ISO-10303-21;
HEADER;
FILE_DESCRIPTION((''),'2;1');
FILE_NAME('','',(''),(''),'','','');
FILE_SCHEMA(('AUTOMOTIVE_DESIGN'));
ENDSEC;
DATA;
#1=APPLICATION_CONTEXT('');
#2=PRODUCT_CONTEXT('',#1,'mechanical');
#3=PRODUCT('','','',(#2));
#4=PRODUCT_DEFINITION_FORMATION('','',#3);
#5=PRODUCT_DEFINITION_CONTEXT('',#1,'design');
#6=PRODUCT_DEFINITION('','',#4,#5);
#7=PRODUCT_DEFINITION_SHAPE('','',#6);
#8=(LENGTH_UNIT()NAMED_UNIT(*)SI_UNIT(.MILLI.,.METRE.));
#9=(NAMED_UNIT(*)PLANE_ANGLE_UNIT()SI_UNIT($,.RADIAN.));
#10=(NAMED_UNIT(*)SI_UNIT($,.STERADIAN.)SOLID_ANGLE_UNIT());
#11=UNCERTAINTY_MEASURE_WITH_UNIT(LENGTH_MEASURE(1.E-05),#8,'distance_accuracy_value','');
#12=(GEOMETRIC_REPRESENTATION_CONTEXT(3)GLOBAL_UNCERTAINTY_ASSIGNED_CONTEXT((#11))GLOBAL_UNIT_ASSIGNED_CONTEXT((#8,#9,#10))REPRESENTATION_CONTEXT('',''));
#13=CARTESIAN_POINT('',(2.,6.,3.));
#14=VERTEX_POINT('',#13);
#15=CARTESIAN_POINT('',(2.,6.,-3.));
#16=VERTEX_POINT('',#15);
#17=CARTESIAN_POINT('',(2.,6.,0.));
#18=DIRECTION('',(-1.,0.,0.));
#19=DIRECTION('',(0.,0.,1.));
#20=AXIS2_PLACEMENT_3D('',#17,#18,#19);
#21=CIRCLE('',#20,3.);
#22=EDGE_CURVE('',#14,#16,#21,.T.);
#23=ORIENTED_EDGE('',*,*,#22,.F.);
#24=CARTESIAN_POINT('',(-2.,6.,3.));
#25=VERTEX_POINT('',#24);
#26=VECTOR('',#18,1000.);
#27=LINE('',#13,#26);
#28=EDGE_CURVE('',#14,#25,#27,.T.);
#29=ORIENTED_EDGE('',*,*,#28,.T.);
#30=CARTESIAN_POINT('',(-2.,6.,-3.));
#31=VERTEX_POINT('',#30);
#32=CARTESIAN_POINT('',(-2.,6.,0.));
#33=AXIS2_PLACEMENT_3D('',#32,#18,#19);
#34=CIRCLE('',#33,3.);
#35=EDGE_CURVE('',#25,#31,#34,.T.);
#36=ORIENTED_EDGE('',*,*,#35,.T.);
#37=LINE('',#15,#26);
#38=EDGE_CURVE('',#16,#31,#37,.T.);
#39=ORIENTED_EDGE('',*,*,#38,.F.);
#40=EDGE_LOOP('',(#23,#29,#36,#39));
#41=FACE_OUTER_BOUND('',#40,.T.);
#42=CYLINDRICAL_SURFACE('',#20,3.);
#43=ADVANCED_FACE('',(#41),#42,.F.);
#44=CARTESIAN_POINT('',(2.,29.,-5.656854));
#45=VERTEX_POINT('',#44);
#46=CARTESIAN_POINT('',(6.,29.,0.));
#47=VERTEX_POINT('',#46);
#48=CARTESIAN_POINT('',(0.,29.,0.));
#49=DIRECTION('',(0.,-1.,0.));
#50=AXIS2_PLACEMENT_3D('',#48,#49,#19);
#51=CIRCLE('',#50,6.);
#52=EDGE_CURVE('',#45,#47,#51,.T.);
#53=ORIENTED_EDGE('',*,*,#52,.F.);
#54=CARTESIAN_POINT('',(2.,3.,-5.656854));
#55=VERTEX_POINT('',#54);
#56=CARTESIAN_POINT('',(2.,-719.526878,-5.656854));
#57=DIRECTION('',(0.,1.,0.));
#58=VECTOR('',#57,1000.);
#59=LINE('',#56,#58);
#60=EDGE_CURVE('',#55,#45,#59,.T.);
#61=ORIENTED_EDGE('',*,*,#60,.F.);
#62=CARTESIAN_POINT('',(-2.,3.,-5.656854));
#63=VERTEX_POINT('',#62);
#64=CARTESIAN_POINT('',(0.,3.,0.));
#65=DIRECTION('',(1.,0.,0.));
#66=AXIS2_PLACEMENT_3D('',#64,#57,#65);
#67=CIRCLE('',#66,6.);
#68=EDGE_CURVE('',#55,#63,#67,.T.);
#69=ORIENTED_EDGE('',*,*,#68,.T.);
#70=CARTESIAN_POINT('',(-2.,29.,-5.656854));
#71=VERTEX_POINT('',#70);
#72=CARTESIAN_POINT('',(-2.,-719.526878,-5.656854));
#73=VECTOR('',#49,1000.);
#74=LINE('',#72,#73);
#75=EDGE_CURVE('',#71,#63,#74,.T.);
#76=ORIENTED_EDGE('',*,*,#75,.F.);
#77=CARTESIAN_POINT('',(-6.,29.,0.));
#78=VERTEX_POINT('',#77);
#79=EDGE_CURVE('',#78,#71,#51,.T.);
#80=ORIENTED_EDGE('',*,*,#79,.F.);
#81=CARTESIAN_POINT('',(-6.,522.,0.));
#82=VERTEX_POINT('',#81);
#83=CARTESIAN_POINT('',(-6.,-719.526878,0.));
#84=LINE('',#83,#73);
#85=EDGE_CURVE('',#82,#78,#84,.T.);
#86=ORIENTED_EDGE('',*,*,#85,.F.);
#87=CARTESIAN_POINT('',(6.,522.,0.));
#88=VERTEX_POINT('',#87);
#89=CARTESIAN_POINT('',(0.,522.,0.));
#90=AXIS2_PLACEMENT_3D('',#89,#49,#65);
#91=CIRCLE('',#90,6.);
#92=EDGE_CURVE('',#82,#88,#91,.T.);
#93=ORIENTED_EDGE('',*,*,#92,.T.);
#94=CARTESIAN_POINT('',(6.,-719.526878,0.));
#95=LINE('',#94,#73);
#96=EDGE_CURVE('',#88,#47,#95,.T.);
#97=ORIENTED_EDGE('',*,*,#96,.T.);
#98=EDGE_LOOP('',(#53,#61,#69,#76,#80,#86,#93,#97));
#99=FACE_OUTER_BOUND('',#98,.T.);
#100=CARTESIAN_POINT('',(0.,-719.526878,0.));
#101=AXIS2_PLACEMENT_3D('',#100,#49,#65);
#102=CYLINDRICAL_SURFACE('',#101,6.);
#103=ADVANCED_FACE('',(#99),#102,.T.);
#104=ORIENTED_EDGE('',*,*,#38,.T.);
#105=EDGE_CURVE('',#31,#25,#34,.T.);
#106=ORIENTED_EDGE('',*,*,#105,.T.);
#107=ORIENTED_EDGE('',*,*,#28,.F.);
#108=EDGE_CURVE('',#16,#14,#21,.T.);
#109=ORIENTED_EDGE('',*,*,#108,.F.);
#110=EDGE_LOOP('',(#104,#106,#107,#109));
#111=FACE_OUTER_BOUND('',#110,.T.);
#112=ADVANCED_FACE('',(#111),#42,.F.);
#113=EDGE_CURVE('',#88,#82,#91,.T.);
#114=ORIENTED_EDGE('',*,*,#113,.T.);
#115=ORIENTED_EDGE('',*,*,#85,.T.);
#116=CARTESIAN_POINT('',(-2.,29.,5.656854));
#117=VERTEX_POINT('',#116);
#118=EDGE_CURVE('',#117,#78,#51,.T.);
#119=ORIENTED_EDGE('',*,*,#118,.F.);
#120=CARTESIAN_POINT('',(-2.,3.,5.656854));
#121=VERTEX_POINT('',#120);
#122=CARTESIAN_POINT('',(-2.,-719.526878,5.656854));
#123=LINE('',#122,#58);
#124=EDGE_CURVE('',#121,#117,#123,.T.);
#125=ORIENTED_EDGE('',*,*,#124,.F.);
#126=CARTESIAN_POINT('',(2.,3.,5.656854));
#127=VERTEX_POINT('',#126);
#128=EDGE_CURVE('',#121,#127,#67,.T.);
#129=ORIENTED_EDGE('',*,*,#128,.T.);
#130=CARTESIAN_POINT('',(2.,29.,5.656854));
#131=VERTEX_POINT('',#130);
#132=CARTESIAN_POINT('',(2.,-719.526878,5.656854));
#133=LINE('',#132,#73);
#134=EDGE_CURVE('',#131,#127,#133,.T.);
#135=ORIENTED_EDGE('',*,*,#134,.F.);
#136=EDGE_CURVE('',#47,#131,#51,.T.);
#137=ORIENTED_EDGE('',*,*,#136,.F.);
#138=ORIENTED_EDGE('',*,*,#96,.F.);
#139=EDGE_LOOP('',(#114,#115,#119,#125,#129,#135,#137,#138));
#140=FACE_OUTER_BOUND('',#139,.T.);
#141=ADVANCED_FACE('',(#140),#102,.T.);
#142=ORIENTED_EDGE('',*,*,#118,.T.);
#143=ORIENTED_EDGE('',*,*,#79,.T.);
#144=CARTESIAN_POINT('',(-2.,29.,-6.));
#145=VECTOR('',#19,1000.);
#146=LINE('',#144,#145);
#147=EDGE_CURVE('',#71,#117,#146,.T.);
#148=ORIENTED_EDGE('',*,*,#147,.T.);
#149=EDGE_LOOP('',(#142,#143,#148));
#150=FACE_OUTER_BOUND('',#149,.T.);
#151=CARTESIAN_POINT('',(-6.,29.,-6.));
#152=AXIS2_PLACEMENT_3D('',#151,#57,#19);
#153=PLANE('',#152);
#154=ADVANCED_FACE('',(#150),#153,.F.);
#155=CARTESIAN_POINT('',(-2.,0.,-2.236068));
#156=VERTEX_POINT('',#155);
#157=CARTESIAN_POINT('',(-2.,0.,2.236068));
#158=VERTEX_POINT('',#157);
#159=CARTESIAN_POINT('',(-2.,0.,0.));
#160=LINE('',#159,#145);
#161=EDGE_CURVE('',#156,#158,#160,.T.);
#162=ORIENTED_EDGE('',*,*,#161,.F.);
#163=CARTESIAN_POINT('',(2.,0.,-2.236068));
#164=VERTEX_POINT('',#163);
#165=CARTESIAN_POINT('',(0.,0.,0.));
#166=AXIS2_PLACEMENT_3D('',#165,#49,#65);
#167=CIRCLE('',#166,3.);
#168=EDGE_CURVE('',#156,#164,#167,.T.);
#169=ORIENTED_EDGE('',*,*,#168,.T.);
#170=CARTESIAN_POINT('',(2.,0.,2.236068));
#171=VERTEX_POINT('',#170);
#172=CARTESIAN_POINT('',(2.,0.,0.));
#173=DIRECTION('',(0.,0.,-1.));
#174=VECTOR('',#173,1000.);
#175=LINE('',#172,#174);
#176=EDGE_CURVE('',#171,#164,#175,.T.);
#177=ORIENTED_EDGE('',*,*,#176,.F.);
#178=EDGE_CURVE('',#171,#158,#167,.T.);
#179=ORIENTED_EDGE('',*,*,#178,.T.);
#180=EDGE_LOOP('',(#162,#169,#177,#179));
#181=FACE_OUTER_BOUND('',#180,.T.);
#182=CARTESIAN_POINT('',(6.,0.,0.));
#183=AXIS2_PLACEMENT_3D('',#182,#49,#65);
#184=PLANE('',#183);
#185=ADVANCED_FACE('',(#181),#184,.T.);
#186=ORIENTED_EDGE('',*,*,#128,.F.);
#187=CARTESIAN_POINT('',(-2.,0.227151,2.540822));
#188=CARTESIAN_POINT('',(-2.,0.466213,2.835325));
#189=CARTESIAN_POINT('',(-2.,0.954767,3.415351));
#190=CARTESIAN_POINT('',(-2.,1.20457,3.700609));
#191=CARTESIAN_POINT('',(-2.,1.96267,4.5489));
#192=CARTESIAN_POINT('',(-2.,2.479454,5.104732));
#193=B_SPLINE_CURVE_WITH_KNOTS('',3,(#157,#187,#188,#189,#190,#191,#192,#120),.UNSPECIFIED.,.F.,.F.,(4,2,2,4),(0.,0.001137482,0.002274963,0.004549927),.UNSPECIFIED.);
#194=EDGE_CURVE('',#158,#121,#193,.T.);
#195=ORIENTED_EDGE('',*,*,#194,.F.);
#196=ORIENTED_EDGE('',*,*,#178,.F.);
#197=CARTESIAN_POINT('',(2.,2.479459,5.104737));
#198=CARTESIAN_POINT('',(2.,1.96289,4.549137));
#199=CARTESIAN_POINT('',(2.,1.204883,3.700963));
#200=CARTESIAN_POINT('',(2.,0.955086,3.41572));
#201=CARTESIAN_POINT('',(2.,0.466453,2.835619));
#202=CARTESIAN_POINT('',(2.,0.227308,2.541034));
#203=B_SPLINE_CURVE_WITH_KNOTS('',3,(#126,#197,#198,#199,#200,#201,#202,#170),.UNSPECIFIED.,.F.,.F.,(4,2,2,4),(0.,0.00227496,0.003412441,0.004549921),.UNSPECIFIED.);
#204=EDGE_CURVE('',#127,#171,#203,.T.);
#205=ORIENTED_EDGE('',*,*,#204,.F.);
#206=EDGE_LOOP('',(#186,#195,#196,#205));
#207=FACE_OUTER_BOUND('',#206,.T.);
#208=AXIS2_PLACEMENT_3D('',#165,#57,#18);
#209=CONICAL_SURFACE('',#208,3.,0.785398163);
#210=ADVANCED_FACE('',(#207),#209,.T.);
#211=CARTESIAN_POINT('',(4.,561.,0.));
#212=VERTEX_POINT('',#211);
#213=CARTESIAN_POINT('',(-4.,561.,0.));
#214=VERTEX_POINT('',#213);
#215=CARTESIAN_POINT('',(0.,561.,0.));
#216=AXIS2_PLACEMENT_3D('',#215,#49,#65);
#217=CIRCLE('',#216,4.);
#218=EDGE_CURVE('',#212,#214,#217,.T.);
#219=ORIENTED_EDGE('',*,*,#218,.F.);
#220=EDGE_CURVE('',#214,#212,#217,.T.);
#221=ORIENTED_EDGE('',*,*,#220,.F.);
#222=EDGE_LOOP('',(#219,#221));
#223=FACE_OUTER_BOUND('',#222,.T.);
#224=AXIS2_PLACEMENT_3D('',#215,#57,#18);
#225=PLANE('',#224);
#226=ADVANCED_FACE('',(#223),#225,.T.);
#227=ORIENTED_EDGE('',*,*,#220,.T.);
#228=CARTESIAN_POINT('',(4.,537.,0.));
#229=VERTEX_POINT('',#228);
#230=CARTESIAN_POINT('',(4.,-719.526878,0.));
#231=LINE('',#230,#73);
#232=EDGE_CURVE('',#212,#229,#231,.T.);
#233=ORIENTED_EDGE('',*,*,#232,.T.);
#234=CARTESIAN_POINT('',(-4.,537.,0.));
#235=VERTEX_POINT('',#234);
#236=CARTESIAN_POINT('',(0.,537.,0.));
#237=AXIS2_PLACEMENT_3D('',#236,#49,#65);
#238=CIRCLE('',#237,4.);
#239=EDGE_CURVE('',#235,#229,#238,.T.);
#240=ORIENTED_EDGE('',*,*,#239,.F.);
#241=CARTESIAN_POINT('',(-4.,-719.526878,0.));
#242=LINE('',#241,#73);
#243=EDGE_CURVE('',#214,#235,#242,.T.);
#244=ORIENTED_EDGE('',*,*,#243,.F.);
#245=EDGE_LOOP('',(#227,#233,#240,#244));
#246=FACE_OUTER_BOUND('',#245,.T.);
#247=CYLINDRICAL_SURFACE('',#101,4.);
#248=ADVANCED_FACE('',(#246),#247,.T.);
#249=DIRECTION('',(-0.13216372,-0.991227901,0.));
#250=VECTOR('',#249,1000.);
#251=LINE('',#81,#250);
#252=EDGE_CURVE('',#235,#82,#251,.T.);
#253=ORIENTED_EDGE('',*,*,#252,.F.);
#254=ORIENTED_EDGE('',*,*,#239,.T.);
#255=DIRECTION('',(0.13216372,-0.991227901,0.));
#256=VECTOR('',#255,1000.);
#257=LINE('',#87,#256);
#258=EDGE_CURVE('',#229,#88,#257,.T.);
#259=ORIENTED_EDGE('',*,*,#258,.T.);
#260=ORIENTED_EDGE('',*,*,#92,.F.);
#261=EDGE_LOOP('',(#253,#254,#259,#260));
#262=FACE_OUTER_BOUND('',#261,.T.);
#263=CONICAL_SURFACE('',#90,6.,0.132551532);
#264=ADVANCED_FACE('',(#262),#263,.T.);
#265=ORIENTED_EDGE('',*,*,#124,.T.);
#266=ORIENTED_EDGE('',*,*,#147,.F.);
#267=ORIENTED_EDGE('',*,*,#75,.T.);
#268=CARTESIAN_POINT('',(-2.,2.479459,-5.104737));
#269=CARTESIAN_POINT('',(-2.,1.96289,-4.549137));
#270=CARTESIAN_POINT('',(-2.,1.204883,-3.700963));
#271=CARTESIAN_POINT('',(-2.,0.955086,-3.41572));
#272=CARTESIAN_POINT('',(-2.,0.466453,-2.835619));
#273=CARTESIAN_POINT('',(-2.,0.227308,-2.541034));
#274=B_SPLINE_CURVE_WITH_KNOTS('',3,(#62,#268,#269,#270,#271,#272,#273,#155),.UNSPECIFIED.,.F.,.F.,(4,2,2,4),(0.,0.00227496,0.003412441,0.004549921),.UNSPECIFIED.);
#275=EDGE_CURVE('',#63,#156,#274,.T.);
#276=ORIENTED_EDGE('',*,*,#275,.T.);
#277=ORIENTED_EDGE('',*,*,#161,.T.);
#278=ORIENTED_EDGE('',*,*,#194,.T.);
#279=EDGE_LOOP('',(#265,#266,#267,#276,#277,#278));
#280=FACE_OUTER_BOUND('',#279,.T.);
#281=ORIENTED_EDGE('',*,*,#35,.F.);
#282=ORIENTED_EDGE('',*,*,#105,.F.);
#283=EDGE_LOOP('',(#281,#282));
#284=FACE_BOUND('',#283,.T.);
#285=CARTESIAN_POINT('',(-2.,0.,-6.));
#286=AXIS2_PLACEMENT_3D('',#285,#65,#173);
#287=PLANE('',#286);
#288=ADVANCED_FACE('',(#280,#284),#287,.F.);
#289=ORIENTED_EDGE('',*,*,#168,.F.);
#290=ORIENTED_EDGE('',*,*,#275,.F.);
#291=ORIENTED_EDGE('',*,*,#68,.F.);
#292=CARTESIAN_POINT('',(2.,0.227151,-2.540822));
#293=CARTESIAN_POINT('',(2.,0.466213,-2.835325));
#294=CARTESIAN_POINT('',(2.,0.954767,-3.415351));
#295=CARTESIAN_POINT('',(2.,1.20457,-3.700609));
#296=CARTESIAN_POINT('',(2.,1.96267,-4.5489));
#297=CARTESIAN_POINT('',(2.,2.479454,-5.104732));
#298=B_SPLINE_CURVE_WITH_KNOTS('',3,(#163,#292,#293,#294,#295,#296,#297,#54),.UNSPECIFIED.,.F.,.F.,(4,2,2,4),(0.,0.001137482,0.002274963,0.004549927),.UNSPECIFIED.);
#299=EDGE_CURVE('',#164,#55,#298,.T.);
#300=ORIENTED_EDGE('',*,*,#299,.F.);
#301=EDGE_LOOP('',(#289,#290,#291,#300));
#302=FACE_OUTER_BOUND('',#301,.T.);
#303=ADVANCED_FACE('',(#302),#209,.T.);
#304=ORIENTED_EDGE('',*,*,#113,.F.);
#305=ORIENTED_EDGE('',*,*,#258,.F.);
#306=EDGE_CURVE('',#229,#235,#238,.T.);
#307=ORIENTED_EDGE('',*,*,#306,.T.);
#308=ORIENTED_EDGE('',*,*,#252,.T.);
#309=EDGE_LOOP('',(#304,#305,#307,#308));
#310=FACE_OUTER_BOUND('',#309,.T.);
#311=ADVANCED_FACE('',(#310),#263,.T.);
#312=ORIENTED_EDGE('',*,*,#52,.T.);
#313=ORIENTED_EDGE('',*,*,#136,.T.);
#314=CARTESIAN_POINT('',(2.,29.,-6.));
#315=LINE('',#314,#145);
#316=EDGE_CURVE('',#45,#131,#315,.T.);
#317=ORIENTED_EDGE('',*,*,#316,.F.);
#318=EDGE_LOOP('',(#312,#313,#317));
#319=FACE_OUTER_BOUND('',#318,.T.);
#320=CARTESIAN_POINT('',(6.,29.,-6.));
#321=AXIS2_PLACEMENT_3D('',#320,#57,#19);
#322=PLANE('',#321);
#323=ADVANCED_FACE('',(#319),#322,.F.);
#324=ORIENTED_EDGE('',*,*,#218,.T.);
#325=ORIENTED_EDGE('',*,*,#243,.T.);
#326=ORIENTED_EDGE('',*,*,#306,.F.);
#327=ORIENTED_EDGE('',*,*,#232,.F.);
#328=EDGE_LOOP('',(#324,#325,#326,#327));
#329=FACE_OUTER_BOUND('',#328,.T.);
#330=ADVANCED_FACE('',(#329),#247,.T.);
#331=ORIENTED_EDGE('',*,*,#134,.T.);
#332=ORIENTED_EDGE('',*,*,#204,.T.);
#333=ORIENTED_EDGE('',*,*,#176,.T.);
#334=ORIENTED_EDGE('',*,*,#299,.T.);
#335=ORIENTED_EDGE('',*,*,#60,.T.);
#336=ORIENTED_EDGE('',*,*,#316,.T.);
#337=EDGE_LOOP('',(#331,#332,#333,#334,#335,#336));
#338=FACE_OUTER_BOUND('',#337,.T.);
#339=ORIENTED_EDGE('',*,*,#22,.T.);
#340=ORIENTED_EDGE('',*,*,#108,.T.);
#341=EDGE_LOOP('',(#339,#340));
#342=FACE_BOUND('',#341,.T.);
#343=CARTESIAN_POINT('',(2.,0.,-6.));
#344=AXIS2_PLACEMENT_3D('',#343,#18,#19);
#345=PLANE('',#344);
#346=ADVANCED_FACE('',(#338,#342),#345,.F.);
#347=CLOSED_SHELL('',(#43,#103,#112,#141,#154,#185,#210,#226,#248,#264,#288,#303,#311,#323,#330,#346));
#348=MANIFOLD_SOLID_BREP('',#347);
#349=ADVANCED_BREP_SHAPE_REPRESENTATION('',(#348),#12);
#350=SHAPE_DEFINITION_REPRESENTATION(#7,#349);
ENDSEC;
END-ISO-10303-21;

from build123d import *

# Parameters (mm, degrees)
CUT_EXTRUDE1_DEPTH      = 562.064167453
CUT_EXTRUDE1_DEPTH_BACK = 562.064167453
SKETCH2_W               = 4
SKETCH2_H               = 29
CUT_EXTRUDE2_DEPTH      = 562.064167453
CUT_EXTRUDE2_DEPTH_BACK = 562.064167453
SKETCH3_W               = 4
SKETCH3_H               = 29
CHAMFER1_SIZE           = 3
SKETCH4_R               = 3
CUT_EXTRUDE3_DEPTH      = 4


with BuildPart() as part:
    # Sketch1 → Revolve1 (revolve)
    with BuildSketch(Plane.XY):
        Polygon((0, 561), (4, 561), (4, 537), (6, 522), (6, 0), (0, 0), align=None)
    revolve(axis=Axis((0, -719.526877718, 0), (0, 1, 0)))

    # Sketch2 → Cut-Extrude1 (cut, two sides: drawn at the far end of the back side and taken through both)
    with BuildSketch(Plane.XY.offset(-CUT_EXTRUDE1_DEPTH_BACK)):
        with Locations((-4, 14.5)):
            Rectangle(SKETCH2_W, SKETCH2_H)
    extrude(amount=CUT_EXTRUDE1_DEPTH + CUT_EXTRUDE1_DEPTH_BACK, mode=Mode.SUBTRACT)

    # Sketch3 → Cut-Extrude2 (cut, two sides: drawn at the far end of the back side and taken through both)
    with BuildSketch(Plane.XY.offset(-CUT_EXTRUDE2_DEPTH_BACK)):
        with Locations((4, 14.5)):
            Rectangle(SKETCH3_W, SKETCH3_H)
    extrude(amount=CUT_EXTRUDE2_DEPTH + CUT_EXTRUDE2_DEPTH_BACK, mode=Mode.SUBTRACT)

    # Chamfer1
    chamfer1_edges = [part.edges().sort_by_distance(p)[0] for p in [
        (0, 0, -6),
        (0, 0, 6),
    ]]
    chamfer(chamfer1_edges, length=CHAMFER1_SIZE)

    # Sketch4 → Cut-Extrude3 (cut)
    with BuildSketch(Plane.ZY.offset(2)):
        with Locations((0, 6)):
            Circle(SKETCH4_R)
    extrude(amount=-CUT_EXTRUDE3_DEPTH, mode=Mode.SUBTRACT)


solid = part.part
